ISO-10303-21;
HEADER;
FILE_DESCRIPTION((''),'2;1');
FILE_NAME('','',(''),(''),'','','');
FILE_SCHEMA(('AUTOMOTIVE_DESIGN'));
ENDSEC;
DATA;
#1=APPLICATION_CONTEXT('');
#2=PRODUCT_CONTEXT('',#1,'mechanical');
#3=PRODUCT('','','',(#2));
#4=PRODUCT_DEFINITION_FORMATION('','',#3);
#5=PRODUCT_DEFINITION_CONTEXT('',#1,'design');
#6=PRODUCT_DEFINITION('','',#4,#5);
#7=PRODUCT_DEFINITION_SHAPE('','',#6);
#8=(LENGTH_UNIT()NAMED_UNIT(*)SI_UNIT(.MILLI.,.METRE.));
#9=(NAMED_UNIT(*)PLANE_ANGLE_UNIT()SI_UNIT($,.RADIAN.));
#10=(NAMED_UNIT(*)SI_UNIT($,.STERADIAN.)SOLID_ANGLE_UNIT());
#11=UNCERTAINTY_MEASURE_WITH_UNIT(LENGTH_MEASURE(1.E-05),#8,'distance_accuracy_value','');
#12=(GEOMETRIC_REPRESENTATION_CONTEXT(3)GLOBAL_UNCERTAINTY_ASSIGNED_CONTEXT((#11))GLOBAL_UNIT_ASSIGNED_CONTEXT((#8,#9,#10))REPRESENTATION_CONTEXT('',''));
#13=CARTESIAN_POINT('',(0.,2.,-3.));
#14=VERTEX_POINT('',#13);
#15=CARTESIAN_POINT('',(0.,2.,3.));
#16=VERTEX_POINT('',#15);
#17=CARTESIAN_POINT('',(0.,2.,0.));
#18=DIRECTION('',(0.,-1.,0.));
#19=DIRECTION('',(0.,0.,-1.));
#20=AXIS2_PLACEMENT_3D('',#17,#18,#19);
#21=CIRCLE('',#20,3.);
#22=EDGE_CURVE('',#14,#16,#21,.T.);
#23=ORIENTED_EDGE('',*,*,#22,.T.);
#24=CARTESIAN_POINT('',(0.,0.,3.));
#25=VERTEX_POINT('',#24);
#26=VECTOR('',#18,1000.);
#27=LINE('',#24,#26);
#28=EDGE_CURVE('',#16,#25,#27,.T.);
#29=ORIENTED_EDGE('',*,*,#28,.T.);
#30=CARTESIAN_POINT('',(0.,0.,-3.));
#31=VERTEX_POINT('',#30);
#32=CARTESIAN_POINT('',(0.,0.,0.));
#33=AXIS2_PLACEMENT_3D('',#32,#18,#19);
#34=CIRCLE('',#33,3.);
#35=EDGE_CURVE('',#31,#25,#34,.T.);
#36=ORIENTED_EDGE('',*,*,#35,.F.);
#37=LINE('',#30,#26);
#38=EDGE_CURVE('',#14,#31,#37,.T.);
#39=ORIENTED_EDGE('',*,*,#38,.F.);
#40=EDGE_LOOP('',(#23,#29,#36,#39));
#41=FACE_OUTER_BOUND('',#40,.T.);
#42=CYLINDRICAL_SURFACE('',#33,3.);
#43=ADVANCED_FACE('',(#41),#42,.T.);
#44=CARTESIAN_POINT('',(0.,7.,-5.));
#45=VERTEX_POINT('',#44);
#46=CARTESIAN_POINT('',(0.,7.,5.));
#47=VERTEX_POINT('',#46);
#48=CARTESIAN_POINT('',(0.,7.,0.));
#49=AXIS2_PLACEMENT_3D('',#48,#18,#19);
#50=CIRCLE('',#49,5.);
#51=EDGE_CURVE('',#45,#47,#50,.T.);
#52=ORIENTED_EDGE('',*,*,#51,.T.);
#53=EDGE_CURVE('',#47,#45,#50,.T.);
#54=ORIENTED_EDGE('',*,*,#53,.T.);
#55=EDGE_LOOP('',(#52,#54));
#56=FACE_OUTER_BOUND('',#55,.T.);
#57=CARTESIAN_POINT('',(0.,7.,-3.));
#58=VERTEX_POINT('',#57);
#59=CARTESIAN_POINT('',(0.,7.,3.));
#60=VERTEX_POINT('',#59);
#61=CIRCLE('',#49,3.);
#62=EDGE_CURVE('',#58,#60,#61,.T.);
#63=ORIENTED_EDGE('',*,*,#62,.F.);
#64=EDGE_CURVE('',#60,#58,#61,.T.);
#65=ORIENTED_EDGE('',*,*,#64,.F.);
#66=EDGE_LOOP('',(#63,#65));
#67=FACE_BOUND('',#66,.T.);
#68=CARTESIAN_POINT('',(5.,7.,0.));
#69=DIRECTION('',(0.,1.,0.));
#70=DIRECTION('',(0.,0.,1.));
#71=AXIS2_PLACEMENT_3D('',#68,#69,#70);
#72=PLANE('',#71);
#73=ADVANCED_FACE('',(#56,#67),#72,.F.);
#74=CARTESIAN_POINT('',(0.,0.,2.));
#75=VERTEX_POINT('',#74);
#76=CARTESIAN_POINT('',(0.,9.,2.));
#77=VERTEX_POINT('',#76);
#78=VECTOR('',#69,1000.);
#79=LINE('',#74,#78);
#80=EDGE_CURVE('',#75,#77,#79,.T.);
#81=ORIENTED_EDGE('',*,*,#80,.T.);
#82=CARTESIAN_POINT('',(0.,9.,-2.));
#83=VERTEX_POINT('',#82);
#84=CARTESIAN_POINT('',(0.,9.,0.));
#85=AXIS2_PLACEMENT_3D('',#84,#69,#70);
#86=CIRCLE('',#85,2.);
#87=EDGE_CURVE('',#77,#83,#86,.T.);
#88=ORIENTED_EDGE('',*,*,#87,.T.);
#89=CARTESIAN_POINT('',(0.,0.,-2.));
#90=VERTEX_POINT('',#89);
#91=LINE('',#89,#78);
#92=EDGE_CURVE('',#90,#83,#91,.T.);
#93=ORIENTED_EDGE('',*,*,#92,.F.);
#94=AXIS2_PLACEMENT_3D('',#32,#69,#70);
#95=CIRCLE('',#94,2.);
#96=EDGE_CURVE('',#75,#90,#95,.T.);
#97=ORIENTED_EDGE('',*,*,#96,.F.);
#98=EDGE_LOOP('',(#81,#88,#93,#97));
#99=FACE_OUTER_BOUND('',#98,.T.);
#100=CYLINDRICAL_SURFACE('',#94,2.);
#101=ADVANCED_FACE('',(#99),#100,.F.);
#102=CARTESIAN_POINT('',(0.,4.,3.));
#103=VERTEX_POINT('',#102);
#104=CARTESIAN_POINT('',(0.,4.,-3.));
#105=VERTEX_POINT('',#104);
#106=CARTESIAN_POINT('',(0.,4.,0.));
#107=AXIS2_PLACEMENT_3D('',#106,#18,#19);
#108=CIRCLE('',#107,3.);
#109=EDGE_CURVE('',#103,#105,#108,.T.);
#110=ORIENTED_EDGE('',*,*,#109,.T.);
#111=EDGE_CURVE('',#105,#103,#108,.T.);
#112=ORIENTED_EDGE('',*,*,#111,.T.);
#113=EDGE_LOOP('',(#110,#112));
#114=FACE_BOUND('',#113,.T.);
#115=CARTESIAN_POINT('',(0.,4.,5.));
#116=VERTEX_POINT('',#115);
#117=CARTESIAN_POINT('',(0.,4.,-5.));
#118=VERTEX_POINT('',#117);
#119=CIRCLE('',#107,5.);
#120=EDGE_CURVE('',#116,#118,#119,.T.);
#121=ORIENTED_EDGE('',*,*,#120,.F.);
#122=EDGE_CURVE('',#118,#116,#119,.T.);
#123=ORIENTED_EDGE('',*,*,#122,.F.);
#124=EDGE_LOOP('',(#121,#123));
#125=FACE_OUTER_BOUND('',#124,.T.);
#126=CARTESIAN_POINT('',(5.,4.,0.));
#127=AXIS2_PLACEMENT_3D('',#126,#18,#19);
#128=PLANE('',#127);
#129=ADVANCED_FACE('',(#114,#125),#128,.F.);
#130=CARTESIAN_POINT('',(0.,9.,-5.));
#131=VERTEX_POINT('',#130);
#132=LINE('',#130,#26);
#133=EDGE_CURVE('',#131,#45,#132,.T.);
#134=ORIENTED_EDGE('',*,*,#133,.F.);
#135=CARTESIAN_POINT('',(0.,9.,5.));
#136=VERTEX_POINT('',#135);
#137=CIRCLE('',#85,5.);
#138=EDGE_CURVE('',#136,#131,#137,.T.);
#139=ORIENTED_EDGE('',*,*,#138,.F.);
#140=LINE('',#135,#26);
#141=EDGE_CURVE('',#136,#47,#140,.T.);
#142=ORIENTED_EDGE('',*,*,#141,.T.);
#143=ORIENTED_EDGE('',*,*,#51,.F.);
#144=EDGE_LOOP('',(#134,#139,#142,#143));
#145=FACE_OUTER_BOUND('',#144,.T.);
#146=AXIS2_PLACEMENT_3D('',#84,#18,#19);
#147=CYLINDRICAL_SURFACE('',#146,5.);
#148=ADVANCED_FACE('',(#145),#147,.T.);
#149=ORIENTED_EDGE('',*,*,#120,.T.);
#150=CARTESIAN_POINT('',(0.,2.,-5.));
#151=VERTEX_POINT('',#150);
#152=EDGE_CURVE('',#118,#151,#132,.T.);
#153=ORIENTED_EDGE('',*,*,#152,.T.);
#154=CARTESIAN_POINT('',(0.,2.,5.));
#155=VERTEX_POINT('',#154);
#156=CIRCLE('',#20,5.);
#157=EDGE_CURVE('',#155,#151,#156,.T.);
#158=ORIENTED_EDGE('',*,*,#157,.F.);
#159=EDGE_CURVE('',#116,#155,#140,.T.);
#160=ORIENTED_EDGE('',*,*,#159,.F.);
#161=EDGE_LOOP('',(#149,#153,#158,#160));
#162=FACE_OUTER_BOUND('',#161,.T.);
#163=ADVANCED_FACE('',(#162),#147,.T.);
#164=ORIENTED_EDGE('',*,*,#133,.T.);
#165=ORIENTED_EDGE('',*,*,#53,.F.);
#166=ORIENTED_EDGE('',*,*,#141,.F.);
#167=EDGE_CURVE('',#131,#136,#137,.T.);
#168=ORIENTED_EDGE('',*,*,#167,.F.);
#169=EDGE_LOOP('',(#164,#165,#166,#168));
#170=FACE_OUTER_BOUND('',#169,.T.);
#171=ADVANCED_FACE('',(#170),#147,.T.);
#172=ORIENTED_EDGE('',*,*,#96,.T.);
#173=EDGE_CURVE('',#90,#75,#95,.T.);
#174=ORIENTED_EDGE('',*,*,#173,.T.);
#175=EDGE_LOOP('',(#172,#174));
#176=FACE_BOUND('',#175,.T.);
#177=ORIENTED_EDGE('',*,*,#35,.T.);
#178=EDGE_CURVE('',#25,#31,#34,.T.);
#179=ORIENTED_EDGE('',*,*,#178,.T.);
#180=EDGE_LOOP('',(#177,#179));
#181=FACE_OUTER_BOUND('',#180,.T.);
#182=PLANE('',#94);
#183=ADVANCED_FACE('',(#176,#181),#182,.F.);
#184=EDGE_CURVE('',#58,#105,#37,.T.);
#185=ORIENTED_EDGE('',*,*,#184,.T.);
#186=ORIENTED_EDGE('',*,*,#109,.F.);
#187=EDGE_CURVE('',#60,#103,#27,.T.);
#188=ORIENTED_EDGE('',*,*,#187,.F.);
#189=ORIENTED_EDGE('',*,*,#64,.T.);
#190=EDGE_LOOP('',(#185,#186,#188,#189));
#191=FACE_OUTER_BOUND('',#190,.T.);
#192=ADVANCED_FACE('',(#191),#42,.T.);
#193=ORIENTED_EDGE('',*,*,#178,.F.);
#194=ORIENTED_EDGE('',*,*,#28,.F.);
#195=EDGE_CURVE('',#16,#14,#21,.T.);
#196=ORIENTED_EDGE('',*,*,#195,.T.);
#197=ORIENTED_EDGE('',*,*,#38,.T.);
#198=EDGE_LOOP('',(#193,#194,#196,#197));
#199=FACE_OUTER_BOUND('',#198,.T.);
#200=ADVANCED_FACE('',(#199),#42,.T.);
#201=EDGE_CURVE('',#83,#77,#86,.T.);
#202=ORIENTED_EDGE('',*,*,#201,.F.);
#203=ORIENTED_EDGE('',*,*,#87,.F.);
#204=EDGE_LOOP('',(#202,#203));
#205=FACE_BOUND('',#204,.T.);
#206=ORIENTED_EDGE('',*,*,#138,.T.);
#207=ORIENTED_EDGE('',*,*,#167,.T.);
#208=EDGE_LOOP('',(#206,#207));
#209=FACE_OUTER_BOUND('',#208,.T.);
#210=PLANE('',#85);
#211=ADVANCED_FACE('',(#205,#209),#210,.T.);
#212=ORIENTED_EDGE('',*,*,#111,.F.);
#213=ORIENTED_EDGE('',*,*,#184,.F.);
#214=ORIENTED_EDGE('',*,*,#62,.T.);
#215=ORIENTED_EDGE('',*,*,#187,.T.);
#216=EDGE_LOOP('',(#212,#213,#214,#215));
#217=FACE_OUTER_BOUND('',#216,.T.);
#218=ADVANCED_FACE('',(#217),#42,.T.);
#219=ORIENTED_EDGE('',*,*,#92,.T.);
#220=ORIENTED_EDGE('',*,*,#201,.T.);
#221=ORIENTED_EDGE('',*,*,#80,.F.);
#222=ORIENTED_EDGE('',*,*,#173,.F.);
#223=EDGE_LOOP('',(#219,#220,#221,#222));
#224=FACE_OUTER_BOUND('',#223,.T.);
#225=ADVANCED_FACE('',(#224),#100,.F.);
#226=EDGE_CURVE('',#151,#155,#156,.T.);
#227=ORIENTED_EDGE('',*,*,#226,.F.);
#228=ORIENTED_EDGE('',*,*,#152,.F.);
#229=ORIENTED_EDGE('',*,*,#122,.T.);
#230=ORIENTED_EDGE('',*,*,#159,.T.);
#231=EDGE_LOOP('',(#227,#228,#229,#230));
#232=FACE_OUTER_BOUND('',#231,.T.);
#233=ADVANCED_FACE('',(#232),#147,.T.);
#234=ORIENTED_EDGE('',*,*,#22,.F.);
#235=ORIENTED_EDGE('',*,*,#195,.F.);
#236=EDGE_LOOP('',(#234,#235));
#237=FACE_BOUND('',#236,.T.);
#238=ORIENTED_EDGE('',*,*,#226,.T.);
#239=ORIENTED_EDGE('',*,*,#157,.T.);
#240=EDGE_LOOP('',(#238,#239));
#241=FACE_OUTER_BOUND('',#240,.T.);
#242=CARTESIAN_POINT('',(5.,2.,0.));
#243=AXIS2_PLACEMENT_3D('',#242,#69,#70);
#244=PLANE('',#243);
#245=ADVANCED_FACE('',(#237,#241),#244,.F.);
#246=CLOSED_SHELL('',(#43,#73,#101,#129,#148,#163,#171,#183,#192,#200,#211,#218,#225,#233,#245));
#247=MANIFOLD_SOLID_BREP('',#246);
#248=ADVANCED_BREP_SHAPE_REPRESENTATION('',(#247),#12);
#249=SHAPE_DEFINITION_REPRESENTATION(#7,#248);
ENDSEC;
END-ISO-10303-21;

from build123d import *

# Parameters (mm, degrees)
SKETCH1_R           = 5
BOSS_EXTRUDE1_DEPTH = 9
SKETCH3_W           = 2
SKETCH3_H           = 3
SKETCH3_H_2         = 2
SKETCH4_R           = 2
CUT_EXTRUDE1_DEPTH  = 12.445523142


with BuildPart() as part:
    # Sketch1 → Boss-Extrude1 (new body)
    with BuildSketch(Plane(origin=(0, 0, 0), x_dir=(1, 0, 0), z_dir=(0, 1, 0))):
        with Locations(Location((0, 0, 0), (0, 0, 270))):
            Circle(SKETCH1_R)
    extrude(amount=BOSS_EXTRUDE1_DEPTH)

    # Sketch3 → Cut-Revolve1 (revolve, cut)
    with BuildSketch(Plane.XY, mode=Mode.PRIVATE) as cut_revolve1_sk:
        with Locations((4, 5.5)):
            Rectangle(SKETCH3_W, SKETCH3_H)
        with Locations((4, 1)):
            Rectangle(SKETCH3_W, SKETCH3_H_2)
    revolve(cut_revolve1_sk.sketch.rotate(Axis((0, 0, 0), (0, 1, 0)), 90), axis=Axis((0, 0, 0), (0, 1, 0)), mode=Mode.SUBTRACT)

    # Sketch4 → Cut-Extrude1 (cut, through all)
    with BuildSketch(Plane(origin=(0, 9, 0), x_dir=(1, 0, 0), z_dir=(0, 1, 0))):
        with Locations(Location((0, 0, 0), (0, 0, 270))):
            Circle(SKETCH4_R)
    extrude(amount=-CUT_EXTRUDE1_DEPTH, mode=Mode.SUBTRACT)


solid = part.part
